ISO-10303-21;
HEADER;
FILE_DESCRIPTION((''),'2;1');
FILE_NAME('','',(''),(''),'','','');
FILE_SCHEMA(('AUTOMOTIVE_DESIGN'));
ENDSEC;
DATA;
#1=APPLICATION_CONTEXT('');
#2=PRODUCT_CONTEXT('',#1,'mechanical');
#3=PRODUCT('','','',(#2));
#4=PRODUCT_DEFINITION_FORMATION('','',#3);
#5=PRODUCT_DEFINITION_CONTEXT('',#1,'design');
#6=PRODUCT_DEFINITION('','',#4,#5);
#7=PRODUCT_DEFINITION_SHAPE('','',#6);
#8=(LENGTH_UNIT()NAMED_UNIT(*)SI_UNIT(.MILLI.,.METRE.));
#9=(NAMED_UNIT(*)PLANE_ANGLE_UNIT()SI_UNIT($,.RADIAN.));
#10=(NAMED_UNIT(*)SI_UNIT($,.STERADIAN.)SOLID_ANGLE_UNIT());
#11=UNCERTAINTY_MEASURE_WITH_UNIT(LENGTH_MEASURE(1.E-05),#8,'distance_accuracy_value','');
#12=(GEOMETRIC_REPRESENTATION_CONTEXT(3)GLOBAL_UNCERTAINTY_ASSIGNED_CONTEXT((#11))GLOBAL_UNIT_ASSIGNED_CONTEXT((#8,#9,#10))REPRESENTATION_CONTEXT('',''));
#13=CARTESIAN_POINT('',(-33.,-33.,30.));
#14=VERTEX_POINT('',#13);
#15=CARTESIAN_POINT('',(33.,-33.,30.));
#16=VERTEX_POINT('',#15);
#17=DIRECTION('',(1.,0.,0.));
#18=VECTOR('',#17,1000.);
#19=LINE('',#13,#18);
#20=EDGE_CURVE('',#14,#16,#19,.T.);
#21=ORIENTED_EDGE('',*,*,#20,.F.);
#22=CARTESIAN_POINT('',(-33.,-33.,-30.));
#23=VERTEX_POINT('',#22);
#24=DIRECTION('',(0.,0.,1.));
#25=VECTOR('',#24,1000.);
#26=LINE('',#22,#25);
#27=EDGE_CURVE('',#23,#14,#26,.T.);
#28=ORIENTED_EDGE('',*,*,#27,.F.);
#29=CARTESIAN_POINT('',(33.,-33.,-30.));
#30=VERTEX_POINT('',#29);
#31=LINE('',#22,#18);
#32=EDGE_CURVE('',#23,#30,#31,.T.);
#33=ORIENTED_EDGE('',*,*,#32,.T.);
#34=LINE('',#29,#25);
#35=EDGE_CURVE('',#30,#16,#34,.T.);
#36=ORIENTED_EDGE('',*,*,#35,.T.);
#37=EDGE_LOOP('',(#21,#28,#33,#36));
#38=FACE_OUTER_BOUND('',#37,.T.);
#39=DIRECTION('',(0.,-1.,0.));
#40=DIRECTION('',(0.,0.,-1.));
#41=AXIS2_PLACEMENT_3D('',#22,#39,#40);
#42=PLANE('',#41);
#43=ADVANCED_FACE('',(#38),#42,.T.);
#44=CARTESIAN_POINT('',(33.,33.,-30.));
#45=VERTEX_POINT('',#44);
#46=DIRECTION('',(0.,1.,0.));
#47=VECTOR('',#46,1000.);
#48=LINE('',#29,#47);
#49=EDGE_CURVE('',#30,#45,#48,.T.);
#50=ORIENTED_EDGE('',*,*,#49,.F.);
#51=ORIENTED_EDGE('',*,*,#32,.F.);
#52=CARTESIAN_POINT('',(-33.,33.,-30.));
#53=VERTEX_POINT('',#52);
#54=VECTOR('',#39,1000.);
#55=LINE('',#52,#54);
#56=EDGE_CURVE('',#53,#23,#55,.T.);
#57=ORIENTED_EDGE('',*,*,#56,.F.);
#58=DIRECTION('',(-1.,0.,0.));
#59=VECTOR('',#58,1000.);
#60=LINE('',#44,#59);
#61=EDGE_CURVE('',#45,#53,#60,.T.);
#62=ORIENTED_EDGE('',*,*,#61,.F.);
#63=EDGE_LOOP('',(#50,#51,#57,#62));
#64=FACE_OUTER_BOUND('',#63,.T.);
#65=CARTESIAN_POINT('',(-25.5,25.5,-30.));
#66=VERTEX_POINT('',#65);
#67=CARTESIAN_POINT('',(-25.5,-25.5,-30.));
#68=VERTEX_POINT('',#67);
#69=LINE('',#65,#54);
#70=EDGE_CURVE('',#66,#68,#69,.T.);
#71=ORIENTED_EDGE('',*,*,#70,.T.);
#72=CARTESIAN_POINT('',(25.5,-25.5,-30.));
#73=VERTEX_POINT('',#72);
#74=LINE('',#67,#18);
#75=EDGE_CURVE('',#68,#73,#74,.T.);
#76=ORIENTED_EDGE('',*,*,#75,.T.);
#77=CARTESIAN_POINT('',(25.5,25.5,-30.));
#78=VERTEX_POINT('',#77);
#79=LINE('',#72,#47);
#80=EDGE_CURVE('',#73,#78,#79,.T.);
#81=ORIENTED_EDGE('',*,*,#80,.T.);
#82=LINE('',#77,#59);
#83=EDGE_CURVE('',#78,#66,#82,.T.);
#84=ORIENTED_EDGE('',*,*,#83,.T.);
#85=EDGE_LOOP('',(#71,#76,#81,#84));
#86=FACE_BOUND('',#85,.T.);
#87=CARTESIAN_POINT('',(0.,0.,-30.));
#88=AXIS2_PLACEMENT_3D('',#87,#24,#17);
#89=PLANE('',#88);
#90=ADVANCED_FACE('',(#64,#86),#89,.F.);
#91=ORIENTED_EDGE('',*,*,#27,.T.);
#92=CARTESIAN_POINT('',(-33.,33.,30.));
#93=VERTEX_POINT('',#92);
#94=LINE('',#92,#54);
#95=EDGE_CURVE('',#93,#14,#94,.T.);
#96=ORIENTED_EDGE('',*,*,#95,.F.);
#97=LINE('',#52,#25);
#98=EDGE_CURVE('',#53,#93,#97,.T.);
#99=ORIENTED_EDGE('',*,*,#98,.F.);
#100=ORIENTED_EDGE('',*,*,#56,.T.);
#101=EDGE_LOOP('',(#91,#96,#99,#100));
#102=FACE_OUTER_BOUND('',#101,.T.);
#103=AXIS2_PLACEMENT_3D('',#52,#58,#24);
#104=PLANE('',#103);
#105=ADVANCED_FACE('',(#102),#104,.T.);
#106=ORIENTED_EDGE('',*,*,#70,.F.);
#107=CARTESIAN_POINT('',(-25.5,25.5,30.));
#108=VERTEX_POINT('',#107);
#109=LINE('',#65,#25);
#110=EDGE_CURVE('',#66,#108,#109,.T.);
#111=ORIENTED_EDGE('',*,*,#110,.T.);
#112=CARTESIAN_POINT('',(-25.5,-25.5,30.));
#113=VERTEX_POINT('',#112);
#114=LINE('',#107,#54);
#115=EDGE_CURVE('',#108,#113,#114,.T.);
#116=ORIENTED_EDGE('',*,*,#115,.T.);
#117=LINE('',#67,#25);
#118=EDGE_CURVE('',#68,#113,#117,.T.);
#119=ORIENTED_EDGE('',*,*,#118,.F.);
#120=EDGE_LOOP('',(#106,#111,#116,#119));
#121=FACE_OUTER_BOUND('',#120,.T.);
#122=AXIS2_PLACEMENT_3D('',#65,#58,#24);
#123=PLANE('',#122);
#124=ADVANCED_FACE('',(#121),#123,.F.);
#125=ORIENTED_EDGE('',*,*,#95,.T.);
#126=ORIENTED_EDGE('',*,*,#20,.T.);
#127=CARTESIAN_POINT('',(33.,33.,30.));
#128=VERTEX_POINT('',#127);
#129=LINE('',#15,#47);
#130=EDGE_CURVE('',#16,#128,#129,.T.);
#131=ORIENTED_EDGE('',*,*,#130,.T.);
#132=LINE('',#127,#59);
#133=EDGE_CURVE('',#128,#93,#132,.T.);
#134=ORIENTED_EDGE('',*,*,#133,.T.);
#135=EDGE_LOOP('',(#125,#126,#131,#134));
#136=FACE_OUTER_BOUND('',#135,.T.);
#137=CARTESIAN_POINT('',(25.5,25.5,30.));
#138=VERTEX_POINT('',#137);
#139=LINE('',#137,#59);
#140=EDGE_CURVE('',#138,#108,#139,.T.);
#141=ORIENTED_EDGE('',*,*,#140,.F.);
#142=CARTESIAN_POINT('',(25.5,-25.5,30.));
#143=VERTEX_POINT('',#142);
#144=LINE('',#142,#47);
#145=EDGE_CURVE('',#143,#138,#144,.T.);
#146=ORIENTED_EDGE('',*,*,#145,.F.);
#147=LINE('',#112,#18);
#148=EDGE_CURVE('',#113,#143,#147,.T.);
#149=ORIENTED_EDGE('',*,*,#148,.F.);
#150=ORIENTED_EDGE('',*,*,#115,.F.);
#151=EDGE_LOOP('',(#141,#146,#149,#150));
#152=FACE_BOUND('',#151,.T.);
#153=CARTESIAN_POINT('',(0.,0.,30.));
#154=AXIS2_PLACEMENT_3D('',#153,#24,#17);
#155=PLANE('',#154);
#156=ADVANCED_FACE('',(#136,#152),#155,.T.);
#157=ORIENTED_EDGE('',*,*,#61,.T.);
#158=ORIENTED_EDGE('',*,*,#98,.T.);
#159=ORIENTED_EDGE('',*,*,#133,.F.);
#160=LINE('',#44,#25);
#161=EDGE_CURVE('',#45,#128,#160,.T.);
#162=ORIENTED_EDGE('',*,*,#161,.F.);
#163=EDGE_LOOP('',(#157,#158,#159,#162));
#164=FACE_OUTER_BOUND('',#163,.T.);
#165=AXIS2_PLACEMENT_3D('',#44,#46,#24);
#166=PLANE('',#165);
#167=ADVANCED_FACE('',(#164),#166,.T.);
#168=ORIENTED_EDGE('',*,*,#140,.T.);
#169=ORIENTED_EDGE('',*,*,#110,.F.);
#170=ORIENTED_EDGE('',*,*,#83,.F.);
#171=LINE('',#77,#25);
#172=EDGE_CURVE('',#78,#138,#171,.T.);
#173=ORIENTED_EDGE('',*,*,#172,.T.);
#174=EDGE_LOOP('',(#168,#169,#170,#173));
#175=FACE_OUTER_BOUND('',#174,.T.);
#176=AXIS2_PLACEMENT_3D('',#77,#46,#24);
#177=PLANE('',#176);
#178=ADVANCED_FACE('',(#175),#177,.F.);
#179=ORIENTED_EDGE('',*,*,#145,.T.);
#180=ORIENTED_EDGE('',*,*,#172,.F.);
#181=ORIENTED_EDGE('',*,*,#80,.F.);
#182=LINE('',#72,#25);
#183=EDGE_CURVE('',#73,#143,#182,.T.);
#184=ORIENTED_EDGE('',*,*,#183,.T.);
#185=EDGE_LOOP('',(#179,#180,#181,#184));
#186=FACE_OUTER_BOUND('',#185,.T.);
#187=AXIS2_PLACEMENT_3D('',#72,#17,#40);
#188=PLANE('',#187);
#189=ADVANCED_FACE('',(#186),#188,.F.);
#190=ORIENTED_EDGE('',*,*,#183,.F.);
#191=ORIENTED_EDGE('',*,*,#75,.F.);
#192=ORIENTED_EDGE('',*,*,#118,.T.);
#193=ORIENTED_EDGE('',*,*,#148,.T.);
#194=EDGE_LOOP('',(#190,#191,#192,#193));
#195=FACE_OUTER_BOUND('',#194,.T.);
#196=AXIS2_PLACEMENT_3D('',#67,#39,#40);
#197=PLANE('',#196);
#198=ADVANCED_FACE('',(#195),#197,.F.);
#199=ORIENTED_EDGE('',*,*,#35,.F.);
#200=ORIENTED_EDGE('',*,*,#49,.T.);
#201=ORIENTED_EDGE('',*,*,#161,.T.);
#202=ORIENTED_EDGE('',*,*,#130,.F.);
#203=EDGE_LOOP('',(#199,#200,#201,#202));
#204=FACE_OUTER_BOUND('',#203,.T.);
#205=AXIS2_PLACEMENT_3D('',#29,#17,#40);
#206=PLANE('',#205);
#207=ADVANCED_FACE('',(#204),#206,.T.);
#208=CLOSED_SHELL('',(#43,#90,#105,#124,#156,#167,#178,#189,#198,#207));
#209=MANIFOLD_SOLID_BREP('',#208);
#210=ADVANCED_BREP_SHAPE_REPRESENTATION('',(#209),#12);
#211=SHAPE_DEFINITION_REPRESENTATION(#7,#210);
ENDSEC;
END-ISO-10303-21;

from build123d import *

# Parameters (mm, degrees)
SKETCH_1_W      = 66
SKETCH_1_H      = 66
SKETCH_1_W_2    = 51
SKETCH_1_H_2    = 51
EXTRUDE_1_DEPTH = 30


with BuildPart() as part:
    # 草图1 → 凸台-拉伸1 (new, symmetric)
    with BuildSketch(Plane.XY):
        Rectangle(SKETCH_1_W, SKETCH_1_H)
        Rectangle(SKETCH_1_W_2, SKETCH_1_H_2, mode=Mode.SUBTRACT)
    extrude(amount=EXTRUDE_1_DEPTH, both=True)


solid = part.part
